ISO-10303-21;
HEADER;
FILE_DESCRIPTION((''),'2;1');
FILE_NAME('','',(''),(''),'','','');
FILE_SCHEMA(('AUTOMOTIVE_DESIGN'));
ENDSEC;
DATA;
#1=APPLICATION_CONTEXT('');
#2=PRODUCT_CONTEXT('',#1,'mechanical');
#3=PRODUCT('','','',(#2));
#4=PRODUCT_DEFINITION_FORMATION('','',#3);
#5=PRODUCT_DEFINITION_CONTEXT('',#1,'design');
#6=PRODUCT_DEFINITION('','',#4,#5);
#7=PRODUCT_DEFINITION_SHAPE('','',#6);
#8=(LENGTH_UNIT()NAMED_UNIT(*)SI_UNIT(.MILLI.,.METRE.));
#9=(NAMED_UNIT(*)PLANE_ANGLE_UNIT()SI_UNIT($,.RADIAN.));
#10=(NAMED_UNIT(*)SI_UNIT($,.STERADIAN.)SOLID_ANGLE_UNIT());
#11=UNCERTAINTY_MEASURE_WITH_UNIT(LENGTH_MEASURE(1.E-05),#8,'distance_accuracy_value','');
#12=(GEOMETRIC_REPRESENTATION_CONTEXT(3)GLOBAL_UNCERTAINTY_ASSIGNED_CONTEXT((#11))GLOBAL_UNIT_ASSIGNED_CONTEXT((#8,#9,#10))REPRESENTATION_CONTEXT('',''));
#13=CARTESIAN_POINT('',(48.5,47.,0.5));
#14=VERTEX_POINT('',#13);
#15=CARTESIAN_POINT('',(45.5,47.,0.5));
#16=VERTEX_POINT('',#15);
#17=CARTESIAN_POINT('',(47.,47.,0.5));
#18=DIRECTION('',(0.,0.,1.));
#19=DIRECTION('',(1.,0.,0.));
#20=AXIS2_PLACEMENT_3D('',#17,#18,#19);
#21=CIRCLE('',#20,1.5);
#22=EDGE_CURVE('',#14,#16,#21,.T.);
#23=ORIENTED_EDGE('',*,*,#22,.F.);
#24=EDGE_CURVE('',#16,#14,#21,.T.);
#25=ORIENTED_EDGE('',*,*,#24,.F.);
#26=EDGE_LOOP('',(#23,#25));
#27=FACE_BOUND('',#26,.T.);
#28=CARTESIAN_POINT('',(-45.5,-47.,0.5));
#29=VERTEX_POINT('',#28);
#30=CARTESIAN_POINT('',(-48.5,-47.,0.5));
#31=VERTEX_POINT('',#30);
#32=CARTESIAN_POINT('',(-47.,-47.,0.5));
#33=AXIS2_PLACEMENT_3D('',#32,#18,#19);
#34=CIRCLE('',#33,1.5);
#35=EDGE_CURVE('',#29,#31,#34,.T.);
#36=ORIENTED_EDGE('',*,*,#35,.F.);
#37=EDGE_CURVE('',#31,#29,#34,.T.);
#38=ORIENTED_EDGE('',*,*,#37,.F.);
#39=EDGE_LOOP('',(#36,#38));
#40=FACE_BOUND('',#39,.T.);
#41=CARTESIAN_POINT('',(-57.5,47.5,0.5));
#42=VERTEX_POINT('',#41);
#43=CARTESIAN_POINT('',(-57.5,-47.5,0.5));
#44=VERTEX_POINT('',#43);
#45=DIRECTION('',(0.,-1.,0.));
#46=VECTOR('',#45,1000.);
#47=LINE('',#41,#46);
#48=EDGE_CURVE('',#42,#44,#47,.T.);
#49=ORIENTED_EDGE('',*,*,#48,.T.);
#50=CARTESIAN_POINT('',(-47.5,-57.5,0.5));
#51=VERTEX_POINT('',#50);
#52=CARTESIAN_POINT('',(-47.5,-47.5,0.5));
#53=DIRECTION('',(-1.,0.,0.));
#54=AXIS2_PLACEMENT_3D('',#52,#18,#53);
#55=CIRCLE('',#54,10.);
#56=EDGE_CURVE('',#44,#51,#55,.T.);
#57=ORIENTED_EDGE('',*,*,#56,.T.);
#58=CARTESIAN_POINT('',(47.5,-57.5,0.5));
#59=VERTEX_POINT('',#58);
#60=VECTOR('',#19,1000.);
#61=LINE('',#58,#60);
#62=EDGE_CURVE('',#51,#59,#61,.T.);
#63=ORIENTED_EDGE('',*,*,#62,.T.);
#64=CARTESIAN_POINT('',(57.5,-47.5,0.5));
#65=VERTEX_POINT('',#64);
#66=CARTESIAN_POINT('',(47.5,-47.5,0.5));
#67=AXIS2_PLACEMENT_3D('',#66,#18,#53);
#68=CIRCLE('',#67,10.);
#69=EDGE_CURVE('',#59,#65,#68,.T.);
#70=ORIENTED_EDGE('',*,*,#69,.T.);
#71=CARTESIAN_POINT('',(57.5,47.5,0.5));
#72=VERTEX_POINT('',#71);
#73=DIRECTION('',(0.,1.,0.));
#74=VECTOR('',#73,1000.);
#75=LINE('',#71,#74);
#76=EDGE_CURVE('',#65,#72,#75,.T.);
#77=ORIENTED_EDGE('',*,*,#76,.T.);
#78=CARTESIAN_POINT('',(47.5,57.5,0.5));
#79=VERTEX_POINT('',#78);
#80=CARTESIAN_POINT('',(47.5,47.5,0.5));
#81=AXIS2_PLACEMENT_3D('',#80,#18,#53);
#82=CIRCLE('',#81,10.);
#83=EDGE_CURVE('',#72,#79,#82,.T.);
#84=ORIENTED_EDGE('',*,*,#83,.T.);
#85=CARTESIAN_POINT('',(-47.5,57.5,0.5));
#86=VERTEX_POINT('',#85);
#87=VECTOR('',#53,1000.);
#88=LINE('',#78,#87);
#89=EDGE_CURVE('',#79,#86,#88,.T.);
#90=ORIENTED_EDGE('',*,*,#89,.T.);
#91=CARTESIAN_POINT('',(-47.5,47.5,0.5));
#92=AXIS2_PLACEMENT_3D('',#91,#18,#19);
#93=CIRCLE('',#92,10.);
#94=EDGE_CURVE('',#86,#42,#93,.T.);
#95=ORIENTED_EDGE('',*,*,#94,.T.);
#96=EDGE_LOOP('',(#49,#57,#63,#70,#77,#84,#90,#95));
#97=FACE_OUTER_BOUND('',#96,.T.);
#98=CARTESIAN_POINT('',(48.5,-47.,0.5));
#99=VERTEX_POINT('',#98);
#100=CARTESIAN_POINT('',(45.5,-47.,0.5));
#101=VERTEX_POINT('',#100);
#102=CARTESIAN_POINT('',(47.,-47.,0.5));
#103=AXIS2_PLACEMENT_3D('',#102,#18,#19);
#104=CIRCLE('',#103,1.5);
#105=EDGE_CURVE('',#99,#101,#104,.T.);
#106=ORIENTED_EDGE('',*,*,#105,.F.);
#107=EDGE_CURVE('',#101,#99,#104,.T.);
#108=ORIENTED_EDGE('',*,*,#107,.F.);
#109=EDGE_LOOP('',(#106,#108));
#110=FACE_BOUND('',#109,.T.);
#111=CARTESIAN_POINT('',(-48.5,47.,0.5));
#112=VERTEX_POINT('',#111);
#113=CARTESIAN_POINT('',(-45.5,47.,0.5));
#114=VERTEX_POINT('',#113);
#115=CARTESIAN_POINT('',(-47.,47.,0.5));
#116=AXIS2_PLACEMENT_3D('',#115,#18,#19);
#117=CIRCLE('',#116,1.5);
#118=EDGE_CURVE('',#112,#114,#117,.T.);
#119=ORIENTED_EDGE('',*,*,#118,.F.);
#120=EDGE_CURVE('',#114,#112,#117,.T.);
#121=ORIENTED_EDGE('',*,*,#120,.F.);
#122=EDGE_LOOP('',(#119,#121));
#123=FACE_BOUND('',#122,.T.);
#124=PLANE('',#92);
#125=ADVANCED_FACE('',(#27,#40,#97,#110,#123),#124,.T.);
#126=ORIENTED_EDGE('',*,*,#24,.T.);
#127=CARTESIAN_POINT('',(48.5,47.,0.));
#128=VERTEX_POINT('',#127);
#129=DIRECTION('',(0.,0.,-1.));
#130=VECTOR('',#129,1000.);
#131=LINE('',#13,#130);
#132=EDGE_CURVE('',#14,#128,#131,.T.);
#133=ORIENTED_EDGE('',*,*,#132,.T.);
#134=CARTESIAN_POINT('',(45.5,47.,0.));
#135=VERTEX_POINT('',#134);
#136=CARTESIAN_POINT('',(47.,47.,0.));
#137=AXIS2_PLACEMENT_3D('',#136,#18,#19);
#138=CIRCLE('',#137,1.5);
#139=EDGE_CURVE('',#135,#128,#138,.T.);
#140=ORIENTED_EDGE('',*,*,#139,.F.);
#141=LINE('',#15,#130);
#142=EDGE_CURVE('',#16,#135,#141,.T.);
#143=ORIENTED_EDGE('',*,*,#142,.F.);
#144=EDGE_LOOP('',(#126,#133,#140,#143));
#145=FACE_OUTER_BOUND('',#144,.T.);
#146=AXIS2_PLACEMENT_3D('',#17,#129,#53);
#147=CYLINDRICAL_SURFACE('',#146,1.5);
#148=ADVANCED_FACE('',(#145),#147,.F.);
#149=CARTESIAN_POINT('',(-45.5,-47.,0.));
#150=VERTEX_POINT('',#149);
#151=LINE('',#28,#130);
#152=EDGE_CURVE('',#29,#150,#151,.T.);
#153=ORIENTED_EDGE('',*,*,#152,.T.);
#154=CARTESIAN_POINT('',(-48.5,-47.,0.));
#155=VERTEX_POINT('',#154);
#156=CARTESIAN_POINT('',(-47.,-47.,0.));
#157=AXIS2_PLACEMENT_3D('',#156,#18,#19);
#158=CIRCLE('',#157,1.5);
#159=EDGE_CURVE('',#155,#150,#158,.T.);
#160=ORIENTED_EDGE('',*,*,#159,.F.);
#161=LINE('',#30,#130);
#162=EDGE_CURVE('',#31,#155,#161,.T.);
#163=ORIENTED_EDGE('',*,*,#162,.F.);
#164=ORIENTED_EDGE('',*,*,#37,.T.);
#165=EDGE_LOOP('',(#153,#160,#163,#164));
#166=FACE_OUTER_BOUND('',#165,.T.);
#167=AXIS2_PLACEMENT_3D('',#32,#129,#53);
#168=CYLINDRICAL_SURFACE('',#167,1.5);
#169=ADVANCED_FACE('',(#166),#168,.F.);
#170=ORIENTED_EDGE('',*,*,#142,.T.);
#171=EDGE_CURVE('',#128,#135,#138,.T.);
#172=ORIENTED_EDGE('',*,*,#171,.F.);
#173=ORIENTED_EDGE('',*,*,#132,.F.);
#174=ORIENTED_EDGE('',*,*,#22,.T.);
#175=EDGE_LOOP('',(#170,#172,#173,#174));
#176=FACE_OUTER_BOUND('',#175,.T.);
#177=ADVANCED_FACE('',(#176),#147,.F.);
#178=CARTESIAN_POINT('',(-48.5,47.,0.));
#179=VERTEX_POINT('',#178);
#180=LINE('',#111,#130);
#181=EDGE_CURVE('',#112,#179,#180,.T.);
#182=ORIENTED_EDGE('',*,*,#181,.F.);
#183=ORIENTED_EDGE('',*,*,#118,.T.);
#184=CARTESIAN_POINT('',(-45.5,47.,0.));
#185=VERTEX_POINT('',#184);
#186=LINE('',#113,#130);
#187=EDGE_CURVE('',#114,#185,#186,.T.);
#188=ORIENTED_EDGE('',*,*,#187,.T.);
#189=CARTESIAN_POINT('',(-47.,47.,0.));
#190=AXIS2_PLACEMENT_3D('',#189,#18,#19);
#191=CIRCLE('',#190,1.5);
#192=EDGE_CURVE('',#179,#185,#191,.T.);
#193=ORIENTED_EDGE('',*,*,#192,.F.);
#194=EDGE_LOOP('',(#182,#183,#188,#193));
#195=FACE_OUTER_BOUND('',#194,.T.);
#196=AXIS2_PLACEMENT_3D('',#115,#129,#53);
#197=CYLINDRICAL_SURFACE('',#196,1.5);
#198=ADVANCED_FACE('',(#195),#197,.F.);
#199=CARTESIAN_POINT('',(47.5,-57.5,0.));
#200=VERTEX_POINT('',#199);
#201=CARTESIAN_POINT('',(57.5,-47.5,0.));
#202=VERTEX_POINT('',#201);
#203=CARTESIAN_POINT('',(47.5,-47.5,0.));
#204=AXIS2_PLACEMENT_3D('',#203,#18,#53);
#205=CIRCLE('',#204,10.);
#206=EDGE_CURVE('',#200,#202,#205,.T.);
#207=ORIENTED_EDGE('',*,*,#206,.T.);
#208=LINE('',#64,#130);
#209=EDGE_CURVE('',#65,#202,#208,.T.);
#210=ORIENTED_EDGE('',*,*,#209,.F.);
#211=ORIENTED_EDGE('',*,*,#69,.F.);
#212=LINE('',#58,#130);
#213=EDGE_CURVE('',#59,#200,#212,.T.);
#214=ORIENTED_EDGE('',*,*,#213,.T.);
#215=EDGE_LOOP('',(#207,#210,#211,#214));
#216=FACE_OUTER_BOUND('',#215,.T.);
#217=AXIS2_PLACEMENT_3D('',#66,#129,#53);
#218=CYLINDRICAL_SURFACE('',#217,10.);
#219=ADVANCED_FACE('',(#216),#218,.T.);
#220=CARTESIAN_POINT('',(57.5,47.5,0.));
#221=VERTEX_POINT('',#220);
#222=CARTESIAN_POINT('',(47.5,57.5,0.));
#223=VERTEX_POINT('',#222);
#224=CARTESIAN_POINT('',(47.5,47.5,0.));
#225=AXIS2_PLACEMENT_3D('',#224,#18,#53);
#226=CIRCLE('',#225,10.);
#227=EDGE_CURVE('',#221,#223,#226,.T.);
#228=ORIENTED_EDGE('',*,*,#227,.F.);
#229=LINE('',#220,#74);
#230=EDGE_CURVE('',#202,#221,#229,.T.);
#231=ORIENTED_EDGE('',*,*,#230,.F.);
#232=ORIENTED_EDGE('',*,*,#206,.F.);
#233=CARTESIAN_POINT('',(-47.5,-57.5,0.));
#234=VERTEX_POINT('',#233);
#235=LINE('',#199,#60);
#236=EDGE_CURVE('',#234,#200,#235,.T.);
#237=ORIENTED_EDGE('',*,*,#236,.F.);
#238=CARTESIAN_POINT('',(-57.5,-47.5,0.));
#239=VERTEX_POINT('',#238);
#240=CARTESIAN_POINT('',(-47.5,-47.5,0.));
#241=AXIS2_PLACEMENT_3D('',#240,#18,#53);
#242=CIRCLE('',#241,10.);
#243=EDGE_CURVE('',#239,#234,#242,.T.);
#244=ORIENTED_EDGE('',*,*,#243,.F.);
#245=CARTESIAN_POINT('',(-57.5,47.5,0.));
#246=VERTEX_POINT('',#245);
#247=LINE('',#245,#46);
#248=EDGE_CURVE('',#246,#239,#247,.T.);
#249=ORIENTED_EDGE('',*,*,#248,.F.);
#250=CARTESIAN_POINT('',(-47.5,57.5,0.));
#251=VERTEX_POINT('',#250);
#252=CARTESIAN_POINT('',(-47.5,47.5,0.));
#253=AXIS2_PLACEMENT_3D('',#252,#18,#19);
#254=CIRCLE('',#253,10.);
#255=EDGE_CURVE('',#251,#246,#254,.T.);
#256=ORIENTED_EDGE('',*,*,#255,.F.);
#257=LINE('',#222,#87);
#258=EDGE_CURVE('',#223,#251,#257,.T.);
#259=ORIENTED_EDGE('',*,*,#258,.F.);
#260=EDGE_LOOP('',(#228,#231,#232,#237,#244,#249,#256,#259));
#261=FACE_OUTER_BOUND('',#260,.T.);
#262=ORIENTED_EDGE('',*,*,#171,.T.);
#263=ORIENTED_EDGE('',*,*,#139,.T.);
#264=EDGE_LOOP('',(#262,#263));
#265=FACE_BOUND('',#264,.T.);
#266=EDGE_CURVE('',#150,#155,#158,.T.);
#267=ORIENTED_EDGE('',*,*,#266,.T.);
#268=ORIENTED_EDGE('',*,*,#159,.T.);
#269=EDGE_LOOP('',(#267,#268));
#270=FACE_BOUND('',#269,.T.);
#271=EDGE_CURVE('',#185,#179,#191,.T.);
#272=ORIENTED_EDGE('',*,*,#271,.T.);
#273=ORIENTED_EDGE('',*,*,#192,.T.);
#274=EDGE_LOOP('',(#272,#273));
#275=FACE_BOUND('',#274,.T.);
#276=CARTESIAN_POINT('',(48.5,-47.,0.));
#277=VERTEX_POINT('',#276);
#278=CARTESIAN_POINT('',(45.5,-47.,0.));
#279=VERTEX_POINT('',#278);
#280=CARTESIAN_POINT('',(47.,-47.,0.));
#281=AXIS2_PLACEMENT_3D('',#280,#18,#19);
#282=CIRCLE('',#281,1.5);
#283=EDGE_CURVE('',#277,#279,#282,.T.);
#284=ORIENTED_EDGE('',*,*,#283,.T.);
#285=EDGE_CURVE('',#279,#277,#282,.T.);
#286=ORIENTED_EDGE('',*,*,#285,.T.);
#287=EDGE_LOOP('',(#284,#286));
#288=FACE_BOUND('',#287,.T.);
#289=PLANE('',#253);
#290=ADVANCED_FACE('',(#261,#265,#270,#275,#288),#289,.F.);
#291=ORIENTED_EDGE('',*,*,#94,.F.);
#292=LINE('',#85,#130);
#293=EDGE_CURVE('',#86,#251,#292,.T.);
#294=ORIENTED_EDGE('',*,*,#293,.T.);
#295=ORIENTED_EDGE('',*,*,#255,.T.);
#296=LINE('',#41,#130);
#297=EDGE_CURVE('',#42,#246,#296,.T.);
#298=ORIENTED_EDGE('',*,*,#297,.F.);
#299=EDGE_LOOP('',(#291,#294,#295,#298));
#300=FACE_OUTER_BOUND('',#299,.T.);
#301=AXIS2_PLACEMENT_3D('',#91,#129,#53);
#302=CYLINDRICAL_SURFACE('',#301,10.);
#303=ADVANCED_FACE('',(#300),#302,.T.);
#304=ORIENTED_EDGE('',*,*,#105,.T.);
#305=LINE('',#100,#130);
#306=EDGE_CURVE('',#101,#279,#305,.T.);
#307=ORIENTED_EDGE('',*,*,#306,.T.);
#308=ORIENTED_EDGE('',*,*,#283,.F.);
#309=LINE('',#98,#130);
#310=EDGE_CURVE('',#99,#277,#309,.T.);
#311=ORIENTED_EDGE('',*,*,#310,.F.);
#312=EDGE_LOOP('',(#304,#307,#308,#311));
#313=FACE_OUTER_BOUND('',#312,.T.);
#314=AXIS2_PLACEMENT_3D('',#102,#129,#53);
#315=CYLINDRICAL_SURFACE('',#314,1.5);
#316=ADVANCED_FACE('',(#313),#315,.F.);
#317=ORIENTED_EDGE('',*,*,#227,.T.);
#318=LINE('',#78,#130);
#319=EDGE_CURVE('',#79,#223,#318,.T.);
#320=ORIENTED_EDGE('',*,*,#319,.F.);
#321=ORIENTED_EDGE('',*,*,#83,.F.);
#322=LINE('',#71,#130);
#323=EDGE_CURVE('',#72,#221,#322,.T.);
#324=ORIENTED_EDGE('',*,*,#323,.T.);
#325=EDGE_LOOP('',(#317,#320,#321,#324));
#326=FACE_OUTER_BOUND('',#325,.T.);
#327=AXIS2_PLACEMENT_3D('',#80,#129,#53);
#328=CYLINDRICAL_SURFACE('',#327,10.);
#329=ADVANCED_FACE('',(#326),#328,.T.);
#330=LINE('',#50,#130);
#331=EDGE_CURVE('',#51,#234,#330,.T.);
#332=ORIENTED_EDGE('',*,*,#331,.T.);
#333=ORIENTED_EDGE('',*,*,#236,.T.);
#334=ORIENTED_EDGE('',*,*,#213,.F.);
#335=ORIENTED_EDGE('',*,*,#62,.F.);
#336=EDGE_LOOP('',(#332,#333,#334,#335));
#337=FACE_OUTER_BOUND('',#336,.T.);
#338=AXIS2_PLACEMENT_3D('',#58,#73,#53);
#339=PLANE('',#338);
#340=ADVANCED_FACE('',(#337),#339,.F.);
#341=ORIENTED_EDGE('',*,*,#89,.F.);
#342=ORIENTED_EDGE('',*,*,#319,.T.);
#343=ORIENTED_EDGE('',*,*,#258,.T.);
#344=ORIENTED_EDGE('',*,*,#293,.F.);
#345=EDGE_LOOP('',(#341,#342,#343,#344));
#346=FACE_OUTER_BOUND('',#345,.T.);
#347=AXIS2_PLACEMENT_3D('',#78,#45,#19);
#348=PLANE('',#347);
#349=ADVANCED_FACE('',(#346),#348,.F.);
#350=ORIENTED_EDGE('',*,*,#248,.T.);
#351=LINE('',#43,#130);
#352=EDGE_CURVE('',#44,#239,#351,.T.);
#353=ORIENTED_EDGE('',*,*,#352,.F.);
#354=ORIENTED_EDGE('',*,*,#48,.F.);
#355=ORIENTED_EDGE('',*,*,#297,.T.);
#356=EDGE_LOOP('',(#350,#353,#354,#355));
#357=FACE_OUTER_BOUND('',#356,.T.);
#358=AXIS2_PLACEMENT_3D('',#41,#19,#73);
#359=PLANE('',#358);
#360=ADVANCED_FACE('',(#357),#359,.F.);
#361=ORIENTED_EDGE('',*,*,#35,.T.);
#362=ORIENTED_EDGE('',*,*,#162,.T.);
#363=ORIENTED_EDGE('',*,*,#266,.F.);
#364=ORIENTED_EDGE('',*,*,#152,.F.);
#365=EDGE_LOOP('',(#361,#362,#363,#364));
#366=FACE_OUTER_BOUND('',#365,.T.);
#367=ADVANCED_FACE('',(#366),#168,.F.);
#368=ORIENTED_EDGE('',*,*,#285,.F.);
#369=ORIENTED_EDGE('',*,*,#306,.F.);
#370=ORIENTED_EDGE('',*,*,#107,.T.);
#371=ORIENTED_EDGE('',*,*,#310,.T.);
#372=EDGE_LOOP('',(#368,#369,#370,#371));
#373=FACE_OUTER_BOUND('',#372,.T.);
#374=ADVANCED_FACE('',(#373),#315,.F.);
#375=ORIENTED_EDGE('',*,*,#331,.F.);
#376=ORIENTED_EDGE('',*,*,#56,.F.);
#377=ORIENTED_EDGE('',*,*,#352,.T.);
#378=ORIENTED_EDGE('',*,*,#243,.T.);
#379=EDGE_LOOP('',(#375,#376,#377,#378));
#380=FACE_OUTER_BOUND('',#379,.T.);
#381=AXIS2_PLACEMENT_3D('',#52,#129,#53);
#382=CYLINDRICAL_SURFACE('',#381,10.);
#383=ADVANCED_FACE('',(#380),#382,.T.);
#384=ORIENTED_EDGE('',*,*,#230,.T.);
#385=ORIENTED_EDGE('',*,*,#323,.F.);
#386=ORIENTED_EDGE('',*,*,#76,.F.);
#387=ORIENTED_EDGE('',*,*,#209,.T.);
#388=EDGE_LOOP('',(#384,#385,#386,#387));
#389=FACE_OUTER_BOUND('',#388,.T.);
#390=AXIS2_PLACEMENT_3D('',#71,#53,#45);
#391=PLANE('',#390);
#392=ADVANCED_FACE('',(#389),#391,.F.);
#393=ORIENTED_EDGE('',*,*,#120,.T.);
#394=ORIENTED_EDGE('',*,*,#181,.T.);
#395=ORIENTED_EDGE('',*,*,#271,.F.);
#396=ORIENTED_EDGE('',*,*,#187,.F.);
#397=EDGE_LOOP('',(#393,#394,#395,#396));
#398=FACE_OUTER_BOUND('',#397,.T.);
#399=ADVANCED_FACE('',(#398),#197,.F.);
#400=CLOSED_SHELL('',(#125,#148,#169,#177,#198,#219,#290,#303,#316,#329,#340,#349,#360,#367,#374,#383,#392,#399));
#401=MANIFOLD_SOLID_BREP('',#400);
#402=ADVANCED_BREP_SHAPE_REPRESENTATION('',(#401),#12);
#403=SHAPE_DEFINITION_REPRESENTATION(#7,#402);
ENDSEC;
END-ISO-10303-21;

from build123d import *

# Parameters (mm, degrees)
SKETCH1_R           = 1.5
BOSS_EXTRUDE1_DEPTH = 0.5


with BuildPart() as part:
    # Sketch1 → Boss-Extrude1 (new body)
    with BuildSketch(Plane.XY):
        with BuildLine():
            Line((47.5, 57.5), (-47.5, 57.5))
            ThreePointArc((-47.5, 57.5), (-54.571067812, 54.571067812), (-57.5, 47.5))
            Line((-57.5, 47.5), (-57.5, -47.5))
            ThreePointArc((-57.5, -47.5), (-54.571067812, -54.571067812), (-47.5, -57.5))
            Line((-47.5, -57.5), (47.5, -57.5))
            ThreePointArc((47.5, -57.5), (54.571067812, -54.571067812), (57.5, -47.5))
            Line((57.5, -47.5), (57.5, 47.5))
            ThreePointArc((57.5, 47.5), (54.571067812, 54.571067812), (47.5, 57.5))
        make_face()
        with Locations((-47, 47)):
            Circle(SKETCH1_R, mode=Mode.SUBTRACT)
        with Locations((47, 47)):
            Circle(SKETCH1_R, mode=Mode.SUBTRACT)
        with Locations((47, -47)):
            Circle(SKETCH1_R, mode=Mode.SUBTRACT)
        with Locations((-47, -47)):
            Circle(SKETCH1_R, mode=Mode.SUBTRACT)
    extrude(amount=BOSS_EXTRUDE1_DEPTH)


solid = part.part
